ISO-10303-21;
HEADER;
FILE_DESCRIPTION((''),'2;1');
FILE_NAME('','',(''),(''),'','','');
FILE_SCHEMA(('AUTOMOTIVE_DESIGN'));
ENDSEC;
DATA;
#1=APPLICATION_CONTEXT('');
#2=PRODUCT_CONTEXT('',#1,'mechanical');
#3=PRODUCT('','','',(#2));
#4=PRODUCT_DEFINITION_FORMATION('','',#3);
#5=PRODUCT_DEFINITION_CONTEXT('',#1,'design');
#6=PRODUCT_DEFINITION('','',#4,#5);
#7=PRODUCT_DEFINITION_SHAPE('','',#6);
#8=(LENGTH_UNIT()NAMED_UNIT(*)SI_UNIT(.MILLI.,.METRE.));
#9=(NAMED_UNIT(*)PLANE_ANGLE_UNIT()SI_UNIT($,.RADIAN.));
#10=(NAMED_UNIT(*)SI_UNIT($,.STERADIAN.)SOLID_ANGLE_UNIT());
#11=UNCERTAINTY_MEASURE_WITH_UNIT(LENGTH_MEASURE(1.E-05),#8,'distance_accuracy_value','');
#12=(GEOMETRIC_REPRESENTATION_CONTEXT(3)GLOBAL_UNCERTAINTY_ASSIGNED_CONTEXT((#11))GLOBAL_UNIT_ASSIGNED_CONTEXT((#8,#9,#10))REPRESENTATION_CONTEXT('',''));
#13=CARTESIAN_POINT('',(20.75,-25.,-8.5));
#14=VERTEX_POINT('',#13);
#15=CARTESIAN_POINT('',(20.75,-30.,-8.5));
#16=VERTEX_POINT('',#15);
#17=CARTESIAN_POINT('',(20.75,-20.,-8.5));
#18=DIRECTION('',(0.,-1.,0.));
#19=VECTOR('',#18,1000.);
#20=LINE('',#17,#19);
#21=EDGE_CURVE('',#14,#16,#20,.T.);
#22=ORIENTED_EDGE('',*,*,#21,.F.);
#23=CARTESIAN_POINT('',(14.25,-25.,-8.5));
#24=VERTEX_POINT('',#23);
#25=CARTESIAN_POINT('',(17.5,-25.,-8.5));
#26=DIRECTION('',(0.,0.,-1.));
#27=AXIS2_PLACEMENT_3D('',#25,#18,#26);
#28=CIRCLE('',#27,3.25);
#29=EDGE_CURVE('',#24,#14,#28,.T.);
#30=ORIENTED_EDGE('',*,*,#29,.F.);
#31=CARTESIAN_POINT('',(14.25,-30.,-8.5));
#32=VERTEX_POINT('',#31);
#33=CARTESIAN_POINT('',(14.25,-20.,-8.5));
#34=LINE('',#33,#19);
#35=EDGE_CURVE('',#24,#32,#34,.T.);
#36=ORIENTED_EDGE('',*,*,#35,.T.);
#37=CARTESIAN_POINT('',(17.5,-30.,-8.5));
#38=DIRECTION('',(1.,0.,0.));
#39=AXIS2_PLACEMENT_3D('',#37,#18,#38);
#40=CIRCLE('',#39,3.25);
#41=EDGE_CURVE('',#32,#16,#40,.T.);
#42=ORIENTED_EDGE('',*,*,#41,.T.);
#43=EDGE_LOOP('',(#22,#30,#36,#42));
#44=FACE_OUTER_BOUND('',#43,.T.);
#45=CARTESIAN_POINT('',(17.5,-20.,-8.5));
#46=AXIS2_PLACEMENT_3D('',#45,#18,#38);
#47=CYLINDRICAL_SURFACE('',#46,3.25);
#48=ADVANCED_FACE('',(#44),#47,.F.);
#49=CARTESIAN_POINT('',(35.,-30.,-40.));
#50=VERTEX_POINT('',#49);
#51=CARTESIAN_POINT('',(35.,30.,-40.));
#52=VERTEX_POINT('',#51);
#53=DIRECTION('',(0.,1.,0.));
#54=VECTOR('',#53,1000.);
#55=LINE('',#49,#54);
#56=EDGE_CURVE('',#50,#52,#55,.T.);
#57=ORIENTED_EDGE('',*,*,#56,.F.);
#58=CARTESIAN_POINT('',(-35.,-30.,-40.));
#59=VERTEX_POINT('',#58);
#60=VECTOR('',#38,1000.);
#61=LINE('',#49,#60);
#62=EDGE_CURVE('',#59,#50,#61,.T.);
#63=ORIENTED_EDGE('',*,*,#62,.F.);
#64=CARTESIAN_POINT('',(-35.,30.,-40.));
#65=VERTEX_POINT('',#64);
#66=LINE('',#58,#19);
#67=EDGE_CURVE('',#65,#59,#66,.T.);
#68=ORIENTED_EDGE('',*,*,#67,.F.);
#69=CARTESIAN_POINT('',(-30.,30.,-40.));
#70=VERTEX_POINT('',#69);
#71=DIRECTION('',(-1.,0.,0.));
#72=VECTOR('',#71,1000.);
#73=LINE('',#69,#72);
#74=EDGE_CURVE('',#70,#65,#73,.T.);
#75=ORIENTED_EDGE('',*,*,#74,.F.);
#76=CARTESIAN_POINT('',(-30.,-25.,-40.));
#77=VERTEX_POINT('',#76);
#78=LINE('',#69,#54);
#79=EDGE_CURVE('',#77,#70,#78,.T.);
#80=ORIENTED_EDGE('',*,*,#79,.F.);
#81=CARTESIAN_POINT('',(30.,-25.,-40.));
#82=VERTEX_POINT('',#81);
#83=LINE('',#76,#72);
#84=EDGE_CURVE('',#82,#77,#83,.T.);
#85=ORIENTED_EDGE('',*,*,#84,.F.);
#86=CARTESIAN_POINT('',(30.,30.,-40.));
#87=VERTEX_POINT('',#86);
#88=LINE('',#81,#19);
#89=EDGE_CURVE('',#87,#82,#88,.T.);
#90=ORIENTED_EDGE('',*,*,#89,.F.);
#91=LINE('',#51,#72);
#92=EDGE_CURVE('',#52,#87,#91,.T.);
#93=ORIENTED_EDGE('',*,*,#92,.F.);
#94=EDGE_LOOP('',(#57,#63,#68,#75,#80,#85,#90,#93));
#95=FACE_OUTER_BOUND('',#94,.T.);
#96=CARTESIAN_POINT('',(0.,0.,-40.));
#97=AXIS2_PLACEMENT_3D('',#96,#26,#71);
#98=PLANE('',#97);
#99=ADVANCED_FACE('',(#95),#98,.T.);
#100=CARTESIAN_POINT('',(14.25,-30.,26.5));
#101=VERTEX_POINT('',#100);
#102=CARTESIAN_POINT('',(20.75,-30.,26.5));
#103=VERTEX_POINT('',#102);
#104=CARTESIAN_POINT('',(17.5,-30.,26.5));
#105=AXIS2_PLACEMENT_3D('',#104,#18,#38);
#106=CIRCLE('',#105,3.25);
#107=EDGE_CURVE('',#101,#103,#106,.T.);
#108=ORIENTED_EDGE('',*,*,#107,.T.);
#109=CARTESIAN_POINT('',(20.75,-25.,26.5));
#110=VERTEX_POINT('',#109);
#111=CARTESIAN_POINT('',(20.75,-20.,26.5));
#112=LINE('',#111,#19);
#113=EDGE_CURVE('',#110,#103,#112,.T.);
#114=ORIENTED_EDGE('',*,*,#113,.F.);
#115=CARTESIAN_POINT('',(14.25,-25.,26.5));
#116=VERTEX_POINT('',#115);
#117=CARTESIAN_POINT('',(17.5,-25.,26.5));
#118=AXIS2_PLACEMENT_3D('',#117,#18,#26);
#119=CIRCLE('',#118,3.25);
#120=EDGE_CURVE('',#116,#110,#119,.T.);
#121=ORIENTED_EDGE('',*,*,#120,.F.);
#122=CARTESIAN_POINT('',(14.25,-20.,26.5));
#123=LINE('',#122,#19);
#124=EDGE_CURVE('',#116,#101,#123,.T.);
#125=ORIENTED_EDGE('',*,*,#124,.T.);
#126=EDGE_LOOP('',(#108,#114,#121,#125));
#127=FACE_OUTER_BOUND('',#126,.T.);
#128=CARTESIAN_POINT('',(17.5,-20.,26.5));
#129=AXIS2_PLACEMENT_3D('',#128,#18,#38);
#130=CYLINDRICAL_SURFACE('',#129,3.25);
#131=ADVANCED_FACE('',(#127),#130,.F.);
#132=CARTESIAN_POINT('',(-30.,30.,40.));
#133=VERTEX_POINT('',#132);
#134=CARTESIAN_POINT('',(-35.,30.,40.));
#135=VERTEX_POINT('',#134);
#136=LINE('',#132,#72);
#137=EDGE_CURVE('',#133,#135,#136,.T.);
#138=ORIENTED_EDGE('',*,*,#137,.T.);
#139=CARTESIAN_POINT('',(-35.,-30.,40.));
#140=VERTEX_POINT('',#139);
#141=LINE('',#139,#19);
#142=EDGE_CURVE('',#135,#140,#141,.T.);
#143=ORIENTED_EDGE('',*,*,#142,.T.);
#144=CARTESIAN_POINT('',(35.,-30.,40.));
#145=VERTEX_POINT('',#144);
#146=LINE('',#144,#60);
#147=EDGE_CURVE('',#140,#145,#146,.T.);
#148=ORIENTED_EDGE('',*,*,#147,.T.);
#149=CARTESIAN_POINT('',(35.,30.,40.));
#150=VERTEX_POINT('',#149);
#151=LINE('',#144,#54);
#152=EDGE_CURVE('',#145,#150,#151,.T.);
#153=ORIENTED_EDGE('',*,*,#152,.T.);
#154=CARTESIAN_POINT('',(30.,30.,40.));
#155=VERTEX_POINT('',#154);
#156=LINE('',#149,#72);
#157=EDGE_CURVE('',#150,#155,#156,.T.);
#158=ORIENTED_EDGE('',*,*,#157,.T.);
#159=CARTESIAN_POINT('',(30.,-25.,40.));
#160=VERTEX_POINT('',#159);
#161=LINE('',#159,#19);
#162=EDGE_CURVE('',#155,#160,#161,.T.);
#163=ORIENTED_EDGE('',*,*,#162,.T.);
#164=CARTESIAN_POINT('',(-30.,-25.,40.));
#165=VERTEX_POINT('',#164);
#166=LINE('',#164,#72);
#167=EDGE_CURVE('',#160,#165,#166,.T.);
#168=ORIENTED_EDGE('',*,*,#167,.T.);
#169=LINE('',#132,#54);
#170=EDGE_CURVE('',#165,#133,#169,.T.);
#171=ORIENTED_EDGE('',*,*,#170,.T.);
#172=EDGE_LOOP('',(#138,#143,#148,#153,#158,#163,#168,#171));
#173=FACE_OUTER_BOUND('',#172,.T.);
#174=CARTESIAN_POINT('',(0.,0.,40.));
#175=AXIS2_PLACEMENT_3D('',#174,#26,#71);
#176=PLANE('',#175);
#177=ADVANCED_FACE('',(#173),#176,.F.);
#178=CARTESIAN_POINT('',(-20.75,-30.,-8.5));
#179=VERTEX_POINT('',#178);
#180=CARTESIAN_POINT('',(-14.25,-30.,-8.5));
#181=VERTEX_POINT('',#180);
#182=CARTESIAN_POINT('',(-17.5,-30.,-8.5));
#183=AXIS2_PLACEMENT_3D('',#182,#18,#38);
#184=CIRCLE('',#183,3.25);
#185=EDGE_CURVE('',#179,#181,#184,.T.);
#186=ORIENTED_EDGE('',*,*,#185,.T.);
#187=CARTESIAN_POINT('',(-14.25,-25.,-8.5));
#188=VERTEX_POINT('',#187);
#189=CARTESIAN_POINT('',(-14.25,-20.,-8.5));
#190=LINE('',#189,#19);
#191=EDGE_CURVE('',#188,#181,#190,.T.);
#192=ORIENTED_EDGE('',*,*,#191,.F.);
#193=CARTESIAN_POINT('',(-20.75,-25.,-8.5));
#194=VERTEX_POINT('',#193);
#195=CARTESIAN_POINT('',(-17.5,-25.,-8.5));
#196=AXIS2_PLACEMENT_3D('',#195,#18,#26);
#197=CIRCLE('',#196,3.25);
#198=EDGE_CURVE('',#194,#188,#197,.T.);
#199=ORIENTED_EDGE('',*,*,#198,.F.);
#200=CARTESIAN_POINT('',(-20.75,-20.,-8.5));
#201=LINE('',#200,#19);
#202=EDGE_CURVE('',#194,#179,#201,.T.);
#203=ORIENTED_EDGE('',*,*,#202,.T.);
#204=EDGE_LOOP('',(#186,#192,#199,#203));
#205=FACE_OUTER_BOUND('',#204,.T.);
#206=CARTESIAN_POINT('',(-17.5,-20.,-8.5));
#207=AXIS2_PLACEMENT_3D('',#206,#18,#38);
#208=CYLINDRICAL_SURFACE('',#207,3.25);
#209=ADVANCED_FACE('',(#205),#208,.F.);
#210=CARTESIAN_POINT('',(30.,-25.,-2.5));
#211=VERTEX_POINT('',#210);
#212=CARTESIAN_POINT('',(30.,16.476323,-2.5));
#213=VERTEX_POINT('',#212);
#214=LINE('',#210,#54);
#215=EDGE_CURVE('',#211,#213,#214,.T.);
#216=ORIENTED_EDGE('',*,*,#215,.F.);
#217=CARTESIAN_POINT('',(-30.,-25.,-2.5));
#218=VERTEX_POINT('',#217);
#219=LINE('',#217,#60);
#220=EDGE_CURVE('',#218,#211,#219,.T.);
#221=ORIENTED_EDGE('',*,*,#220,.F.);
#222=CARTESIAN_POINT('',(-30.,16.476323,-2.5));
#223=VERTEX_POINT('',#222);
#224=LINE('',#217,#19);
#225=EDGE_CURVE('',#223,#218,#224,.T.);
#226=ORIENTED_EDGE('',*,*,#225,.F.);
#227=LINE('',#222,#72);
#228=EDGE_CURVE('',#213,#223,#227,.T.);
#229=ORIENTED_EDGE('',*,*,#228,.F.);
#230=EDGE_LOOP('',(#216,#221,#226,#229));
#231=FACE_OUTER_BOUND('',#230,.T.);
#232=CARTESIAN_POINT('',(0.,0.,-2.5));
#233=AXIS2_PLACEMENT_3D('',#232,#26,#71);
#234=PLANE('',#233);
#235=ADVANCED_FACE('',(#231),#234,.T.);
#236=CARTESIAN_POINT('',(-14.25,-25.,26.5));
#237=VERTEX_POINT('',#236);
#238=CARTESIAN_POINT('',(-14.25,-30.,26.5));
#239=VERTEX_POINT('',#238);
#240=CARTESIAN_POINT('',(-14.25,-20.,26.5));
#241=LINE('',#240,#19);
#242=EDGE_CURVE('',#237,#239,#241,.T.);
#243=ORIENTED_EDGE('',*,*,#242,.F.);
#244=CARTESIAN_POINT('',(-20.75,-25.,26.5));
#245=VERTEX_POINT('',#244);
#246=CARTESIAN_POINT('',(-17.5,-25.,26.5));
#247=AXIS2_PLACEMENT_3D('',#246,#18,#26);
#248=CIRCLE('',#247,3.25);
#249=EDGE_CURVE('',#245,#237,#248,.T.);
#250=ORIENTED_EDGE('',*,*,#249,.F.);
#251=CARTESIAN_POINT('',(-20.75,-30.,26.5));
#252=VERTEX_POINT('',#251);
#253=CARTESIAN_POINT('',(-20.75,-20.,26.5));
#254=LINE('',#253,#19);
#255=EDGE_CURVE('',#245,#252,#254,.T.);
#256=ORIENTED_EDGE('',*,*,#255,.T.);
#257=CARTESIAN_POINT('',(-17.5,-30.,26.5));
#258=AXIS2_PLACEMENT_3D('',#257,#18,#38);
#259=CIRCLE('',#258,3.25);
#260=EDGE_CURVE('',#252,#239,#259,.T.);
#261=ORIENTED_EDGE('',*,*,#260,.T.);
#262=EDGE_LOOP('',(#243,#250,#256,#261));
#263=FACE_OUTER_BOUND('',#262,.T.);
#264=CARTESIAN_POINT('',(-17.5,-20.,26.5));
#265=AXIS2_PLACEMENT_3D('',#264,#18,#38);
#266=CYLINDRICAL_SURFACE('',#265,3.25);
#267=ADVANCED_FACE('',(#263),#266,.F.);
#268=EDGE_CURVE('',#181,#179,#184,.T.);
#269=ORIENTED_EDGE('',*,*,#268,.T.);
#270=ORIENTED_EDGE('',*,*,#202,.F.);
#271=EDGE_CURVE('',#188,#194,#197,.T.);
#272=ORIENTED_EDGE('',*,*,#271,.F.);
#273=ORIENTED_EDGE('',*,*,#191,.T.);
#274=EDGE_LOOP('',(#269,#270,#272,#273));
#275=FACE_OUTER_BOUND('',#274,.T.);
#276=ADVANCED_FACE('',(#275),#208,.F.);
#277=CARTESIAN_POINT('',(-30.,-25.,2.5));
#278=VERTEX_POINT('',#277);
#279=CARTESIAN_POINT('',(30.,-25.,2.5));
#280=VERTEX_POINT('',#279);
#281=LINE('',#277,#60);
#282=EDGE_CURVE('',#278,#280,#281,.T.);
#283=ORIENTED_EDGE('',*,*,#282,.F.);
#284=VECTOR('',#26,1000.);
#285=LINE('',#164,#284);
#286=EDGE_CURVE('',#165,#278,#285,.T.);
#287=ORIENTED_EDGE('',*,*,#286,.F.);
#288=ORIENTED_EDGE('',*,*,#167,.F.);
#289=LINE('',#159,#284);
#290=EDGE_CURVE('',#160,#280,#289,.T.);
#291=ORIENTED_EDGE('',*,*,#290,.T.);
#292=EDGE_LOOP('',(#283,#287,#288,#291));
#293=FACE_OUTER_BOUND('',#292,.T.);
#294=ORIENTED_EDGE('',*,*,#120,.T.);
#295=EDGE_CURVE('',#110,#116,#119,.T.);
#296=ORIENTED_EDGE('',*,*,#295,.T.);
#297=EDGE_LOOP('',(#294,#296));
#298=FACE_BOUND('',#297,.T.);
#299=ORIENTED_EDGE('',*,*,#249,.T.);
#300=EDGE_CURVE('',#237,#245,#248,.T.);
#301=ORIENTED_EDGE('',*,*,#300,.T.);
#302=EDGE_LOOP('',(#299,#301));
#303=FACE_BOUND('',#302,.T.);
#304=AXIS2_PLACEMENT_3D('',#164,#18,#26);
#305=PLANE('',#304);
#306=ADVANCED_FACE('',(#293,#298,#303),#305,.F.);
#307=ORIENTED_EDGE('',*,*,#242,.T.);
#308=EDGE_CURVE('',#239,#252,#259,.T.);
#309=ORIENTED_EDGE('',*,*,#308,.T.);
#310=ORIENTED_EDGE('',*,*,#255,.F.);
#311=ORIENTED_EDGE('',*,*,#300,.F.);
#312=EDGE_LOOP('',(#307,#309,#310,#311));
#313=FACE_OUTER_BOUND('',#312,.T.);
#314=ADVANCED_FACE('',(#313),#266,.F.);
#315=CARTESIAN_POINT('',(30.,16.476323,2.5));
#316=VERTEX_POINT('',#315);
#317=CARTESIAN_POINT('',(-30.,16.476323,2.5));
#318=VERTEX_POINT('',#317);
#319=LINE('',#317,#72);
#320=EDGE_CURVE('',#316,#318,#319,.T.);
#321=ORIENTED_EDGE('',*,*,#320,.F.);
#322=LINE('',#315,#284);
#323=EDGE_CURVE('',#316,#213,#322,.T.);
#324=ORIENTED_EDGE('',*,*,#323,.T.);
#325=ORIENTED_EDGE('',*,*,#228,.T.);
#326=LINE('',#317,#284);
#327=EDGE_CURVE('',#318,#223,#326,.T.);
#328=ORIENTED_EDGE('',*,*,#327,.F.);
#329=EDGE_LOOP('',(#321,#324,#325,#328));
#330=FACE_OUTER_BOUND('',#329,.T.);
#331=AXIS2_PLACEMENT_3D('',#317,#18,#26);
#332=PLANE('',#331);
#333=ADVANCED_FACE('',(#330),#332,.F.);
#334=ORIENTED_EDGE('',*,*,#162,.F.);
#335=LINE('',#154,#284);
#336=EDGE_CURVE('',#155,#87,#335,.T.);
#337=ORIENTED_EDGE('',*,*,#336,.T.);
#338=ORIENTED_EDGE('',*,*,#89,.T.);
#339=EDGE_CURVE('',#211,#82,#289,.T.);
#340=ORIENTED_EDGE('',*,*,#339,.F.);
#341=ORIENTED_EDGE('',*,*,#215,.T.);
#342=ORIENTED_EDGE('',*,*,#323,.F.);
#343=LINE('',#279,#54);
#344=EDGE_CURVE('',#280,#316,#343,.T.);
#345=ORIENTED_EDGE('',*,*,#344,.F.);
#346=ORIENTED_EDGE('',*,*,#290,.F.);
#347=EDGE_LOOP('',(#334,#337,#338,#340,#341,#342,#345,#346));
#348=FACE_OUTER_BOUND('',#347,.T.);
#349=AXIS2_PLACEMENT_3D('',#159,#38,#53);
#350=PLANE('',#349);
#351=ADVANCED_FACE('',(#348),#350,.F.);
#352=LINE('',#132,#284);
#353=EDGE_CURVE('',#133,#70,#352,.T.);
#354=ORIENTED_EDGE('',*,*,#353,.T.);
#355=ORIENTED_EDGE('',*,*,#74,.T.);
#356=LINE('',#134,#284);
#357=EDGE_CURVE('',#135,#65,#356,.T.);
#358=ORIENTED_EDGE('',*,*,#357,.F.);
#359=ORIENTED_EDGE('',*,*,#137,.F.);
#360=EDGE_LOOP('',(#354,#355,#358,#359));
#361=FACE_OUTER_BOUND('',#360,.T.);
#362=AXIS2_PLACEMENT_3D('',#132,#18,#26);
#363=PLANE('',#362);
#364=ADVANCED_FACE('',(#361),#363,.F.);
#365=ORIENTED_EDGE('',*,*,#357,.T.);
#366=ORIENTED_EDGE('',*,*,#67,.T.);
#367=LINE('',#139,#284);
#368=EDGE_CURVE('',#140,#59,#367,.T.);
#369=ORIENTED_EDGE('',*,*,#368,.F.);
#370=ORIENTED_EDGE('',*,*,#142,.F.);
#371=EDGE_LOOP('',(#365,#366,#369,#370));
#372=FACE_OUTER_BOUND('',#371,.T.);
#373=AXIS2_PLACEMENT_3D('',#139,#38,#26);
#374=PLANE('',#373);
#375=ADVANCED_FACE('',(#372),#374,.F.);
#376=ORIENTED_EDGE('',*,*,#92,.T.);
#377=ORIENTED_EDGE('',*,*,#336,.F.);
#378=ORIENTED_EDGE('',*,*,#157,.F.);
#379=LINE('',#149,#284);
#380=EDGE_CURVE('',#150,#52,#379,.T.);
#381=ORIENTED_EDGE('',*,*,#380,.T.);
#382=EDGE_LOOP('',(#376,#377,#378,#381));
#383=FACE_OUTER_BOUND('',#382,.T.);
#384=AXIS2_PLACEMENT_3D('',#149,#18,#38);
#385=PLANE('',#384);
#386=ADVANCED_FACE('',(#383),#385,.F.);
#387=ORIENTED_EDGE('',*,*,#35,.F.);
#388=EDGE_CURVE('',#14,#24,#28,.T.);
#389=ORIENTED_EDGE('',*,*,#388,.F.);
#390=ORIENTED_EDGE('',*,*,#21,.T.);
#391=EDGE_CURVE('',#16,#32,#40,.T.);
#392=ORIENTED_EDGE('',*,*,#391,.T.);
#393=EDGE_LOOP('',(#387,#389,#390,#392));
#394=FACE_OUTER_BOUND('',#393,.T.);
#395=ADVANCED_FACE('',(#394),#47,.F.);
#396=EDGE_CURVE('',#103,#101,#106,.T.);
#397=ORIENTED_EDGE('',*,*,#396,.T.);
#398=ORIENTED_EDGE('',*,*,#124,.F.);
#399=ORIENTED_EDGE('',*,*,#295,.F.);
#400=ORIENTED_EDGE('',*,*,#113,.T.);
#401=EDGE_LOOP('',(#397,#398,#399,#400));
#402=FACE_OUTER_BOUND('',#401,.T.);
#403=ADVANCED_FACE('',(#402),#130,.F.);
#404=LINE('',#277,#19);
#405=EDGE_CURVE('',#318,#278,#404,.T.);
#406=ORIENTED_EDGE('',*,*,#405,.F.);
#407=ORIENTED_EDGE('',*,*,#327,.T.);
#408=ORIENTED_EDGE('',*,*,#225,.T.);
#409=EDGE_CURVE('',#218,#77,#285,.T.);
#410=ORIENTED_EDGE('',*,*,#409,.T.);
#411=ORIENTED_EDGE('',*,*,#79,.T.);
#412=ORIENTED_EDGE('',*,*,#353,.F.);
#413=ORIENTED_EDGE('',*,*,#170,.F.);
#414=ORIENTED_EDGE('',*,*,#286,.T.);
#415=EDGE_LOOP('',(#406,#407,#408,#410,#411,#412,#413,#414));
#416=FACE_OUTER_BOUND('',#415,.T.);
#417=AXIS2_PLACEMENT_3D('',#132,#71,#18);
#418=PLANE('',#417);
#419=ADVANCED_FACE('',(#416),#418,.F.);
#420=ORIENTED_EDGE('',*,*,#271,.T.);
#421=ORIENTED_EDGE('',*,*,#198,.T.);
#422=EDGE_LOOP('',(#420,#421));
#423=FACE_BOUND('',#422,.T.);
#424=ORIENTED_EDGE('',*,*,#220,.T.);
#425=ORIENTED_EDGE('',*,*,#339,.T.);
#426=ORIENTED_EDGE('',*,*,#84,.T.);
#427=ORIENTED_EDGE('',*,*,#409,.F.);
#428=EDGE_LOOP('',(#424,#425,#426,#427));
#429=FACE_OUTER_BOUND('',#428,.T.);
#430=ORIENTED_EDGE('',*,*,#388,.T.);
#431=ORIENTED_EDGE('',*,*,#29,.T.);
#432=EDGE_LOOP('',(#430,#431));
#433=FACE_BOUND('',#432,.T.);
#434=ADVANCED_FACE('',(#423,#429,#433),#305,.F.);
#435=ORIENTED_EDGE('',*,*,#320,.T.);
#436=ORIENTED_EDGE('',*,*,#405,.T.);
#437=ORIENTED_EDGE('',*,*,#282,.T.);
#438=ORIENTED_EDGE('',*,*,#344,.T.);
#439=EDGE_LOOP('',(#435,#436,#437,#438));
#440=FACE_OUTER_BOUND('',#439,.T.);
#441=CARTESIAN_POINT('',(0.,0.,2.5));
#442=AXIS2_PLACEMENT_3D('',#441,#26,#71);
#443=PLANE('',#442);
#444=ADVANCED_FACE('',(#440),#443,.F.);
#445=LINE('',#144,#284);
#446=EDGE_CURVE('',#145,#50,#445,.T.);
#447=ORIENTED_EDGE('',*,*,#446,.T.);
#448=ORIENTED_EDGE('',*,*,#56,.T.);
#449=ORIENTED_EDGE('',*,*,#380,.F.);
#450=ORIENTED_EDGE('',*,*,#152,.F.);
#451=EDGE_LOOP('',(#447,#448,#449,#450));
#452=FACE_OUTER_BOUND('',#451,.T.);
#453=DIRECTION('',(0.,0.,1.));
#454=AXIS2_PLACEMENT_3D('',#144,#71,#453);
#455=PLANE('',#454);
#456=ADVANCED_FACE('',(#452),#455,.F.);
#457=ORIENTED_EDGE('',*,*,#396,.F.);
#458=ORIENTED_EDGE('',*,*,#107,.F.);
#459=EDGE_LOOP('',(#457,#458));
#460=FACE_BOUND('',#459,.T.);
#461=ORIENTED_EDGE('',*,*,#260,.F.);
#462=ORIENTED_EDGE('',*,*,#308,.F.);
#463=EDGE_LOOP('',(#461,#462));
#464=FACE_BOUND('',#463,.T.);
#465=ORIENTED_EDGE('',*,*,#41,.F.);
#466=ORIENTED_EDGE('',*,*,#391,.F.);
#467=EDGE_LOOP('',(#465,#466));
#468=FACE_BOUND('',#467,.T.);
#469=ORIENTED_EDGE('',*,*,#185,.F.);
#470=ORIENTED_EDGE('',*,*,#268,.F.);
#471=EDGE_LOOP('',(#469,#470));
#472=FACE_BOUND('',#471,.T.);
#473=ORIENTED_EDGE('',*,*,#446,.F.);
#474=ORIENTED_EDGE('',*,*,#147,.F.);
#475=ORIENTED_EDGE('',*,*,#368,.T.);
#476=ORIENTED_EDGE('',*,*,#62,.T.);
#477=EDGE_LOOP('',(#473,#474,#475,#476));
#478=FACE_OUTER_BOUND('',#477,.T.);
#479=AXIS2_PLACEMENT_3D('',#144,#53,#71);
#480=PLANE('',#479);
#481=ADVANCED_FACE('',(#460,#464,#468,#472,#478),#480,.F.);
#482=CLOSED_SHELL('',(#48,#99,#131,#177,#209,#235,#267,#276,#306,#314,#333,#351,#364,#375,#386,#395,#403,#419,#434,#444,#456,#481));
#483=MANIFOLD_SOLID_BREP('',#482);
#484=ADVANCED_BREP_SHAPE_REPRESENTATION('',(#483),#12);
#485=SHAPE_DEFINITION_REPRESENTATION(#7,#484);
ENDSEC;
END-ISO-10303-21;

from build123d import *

# Parameters (mm, degrees)
EXTRUDE_1_DEPTH     = 40
SKETCH_2_W          = 60
SKETCH_2_H          = 41.476322839
EXTRUDE_2_DEPTH     = 2.5
SKETCH_3_R          = 3.25
CUT_EXTRUDE_1_DEPTH = 10


with BuildPart() as part:
    # 草图1 → 凸台-拉伸1 (new, symmetric)
    with BuildSketch(Plane.XY):
        Polygon((-30, 30), (-30, -25), (30, -25), (30, 30), (35, 30), (35, -30), (-35, -30), (-35, 30), align=None)
    extrude(amount=EXTRUDE_1_DEPTH, both=True)

    # 草图2 → 凸台-拉伸2 (add, symmetric)
    with BuildSketch(Plane.XY):
        with Locations((0, -4.26183858)):
            Rectangle(SKETCH_2_W, SKETCH_2_H)
    extrude(amount=EXTRUDE_2_DEPTH, both=True)

    # 草图3 → 切除-拉伸1 (cut)
    with BuildSketch(Plane.XZ.offset(30)):
        with Locations((17.5, 26.5)):
            Circle(SKETCH_3_R)
        with Locations((17.5, -8.5)):
            Circle(SKETCH_3_R)
        with Locations((-17.5, -8.5)):
            Circle(SKETCH_3_R)
        with Locations((-17.5, 26.5)):
            Circle(SKETCH_3_R)
    extrude(amount=-CUT_EXTRUDE_1_DEPTH, mode=Mode.SUBTRACT)


solid = part.part
